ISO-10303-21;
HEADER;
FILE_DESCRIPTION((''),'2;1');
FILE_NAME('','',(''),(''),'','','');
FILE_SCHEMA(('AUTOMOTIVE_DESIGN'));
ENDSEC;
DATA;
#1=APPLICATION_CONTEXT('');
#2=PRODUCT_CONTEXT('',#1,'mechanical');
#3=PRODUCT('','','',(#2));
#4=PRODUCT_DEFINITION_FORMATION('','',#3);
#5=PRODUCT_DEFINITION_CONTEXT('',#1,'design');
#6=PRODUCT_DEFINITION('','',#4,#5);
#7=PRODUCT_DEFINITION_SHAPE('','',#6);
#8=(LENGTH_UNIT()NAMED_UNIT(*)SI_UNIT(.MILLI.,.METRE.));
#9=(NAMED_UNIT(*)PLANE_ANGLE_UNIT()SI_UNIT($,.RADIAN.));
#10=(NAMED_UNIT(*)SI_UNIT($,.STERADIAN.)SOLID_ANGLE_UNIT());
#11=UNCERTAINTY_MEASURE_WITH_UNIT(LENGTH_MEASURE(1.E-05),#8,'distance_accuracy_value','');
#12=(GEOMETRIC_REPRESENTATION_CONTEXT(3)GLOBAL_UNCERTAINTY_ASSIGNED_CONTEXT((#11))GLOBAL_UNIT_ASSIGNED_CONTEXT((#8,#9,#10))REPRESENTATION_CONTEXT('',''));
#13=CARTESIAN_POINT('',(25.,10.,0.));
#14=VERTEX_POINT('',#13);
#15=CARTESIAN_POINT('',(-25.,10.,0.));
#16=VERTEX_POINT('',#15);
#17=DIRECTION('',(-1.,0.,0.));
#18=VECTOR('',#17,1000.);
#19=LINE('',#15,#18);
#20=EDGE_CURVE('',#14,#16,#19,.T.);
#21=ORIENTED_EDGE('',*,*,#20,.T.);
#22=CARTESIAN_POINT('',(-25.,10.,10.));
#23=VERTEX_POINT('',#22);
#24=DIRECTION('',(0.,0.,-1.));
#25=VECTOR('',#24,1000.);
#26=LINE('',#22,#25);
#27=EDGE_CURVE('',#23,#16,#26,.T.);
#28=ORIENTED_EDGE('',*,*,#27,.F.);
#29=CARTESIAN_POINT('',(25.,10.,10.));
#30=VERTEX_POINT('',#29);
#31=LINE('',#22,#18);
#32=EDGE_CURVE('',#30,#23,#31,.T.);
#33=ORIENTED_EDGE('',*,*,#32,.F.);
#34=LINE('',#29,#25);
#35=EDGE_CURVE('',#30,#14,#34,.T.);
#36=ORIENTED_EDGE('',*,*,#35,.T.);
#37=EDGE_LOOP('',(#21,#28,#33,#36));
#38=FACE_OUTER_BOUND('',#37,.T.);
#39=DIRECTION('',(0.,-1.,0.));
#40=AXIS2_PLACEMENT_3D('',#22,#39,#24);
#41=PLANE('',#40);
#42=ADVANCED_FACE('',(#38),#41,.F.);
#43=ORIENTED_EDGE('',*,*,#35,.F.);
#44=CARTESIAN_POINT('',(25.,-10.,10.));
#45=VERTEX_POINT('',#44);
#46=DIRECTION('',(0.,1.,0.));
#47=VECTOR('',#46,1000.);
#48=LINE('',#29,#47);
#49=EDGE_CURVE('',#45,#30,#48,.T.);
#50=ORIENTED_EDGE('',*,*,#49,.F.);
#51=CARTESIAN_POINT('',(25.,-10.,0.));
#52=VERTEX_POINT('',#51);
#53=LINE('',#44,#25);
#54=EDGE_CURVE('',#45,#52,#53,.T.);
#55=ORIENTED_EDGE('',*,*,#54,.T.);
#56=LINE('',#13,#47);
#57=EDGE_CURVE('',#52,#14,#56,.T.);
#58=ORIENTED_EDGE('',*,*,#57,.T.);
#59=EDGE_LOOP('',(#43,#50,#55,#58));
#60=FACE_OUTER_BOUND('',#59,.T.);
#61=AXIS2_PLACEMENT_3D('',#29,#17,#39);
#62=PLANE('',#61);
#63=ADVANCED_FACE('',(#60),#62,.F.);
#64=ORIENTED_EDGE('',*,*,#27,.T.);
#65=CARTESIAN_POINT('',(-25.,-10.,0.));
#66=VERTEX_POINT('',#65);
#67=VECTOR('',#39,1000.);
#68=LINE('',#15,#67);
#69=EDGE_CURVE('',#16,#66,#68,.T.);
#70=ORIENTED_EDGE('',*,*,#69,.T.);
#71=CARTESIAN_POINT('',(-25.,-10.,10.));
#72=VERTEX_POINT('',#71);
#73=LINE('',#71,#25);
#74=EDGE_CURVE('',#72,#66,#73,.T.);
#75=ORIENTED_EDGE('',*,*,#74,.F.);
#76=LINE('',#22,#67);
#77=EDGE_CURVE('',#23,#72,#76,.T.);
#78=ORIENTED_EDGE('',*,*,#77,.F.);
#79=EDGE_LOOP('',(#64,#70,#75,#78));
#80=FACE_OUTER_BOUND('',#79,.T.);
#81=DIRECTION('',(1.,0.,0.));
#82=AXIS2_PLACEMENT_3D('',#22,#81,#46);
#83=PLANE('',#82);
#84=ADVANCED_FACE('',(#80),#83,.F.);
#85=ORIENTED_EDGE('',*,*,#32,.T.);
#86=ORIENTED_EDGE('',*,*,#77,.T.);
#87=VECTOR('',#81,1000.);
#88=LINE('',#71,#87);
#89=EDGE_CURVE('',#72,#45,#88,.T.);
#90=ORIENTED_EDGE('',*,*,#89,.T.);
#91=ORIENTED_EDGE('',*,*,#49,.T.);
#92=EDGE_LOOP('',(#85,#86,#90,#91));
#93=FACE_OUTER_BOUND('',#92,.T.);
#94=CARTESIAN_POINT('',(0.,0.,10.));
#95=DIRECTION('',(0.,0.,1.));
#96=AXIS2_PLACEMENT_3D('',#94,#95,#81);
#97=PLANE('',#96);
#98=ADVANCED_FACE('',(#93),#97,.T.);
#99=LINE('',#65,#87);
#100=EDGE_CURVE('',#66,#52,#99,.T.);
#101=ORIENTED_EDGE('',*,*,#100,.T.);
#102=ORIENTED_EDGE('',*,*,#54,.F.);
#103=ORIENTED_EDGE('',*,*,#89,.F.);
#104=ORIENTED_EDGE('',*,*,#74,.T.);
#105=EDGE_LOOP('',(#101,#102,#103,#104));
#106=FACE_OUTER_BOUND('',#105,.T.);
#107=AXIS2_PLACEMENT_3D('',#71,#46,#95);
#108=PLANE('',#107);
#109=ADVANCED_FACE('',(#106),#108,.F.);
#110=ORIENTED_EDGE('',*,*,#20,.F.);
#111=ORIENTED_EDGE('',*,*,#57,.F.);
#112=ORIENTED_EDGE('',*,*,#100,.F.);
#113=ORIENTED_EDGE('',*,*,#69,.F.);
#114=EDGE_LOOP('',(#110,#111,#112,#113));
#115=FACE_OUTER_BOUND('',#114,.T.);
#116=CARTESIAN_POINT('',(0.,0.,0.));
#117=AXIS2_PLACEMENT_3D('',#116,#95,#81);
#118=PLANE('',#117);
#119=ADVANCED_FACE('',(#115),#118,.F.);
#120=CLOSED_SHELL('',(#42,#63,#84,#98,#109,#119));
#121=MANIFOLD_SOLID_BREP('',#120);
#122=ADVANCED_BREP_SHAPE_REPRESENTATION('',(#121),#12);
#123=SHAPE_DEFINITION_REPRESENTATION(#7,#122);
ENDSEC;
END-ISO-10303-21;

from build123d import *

# Parameters (mm, degrees)
SKETCH1_W           = 50
SKETCH1_H           = 20
BOSS_EXTRUDE1_DEPTH = 10


with BuildPart() as part:
    # Sketch1 → Boss-Extrude1 (new body)
    with BuildSketch(Plane.XY):
        Rectangle(SKETCH1_W, SKETCH1_H)
    extrude(amount=BOSS_EXTRUDE1_DEPTH)


solid = part.part
